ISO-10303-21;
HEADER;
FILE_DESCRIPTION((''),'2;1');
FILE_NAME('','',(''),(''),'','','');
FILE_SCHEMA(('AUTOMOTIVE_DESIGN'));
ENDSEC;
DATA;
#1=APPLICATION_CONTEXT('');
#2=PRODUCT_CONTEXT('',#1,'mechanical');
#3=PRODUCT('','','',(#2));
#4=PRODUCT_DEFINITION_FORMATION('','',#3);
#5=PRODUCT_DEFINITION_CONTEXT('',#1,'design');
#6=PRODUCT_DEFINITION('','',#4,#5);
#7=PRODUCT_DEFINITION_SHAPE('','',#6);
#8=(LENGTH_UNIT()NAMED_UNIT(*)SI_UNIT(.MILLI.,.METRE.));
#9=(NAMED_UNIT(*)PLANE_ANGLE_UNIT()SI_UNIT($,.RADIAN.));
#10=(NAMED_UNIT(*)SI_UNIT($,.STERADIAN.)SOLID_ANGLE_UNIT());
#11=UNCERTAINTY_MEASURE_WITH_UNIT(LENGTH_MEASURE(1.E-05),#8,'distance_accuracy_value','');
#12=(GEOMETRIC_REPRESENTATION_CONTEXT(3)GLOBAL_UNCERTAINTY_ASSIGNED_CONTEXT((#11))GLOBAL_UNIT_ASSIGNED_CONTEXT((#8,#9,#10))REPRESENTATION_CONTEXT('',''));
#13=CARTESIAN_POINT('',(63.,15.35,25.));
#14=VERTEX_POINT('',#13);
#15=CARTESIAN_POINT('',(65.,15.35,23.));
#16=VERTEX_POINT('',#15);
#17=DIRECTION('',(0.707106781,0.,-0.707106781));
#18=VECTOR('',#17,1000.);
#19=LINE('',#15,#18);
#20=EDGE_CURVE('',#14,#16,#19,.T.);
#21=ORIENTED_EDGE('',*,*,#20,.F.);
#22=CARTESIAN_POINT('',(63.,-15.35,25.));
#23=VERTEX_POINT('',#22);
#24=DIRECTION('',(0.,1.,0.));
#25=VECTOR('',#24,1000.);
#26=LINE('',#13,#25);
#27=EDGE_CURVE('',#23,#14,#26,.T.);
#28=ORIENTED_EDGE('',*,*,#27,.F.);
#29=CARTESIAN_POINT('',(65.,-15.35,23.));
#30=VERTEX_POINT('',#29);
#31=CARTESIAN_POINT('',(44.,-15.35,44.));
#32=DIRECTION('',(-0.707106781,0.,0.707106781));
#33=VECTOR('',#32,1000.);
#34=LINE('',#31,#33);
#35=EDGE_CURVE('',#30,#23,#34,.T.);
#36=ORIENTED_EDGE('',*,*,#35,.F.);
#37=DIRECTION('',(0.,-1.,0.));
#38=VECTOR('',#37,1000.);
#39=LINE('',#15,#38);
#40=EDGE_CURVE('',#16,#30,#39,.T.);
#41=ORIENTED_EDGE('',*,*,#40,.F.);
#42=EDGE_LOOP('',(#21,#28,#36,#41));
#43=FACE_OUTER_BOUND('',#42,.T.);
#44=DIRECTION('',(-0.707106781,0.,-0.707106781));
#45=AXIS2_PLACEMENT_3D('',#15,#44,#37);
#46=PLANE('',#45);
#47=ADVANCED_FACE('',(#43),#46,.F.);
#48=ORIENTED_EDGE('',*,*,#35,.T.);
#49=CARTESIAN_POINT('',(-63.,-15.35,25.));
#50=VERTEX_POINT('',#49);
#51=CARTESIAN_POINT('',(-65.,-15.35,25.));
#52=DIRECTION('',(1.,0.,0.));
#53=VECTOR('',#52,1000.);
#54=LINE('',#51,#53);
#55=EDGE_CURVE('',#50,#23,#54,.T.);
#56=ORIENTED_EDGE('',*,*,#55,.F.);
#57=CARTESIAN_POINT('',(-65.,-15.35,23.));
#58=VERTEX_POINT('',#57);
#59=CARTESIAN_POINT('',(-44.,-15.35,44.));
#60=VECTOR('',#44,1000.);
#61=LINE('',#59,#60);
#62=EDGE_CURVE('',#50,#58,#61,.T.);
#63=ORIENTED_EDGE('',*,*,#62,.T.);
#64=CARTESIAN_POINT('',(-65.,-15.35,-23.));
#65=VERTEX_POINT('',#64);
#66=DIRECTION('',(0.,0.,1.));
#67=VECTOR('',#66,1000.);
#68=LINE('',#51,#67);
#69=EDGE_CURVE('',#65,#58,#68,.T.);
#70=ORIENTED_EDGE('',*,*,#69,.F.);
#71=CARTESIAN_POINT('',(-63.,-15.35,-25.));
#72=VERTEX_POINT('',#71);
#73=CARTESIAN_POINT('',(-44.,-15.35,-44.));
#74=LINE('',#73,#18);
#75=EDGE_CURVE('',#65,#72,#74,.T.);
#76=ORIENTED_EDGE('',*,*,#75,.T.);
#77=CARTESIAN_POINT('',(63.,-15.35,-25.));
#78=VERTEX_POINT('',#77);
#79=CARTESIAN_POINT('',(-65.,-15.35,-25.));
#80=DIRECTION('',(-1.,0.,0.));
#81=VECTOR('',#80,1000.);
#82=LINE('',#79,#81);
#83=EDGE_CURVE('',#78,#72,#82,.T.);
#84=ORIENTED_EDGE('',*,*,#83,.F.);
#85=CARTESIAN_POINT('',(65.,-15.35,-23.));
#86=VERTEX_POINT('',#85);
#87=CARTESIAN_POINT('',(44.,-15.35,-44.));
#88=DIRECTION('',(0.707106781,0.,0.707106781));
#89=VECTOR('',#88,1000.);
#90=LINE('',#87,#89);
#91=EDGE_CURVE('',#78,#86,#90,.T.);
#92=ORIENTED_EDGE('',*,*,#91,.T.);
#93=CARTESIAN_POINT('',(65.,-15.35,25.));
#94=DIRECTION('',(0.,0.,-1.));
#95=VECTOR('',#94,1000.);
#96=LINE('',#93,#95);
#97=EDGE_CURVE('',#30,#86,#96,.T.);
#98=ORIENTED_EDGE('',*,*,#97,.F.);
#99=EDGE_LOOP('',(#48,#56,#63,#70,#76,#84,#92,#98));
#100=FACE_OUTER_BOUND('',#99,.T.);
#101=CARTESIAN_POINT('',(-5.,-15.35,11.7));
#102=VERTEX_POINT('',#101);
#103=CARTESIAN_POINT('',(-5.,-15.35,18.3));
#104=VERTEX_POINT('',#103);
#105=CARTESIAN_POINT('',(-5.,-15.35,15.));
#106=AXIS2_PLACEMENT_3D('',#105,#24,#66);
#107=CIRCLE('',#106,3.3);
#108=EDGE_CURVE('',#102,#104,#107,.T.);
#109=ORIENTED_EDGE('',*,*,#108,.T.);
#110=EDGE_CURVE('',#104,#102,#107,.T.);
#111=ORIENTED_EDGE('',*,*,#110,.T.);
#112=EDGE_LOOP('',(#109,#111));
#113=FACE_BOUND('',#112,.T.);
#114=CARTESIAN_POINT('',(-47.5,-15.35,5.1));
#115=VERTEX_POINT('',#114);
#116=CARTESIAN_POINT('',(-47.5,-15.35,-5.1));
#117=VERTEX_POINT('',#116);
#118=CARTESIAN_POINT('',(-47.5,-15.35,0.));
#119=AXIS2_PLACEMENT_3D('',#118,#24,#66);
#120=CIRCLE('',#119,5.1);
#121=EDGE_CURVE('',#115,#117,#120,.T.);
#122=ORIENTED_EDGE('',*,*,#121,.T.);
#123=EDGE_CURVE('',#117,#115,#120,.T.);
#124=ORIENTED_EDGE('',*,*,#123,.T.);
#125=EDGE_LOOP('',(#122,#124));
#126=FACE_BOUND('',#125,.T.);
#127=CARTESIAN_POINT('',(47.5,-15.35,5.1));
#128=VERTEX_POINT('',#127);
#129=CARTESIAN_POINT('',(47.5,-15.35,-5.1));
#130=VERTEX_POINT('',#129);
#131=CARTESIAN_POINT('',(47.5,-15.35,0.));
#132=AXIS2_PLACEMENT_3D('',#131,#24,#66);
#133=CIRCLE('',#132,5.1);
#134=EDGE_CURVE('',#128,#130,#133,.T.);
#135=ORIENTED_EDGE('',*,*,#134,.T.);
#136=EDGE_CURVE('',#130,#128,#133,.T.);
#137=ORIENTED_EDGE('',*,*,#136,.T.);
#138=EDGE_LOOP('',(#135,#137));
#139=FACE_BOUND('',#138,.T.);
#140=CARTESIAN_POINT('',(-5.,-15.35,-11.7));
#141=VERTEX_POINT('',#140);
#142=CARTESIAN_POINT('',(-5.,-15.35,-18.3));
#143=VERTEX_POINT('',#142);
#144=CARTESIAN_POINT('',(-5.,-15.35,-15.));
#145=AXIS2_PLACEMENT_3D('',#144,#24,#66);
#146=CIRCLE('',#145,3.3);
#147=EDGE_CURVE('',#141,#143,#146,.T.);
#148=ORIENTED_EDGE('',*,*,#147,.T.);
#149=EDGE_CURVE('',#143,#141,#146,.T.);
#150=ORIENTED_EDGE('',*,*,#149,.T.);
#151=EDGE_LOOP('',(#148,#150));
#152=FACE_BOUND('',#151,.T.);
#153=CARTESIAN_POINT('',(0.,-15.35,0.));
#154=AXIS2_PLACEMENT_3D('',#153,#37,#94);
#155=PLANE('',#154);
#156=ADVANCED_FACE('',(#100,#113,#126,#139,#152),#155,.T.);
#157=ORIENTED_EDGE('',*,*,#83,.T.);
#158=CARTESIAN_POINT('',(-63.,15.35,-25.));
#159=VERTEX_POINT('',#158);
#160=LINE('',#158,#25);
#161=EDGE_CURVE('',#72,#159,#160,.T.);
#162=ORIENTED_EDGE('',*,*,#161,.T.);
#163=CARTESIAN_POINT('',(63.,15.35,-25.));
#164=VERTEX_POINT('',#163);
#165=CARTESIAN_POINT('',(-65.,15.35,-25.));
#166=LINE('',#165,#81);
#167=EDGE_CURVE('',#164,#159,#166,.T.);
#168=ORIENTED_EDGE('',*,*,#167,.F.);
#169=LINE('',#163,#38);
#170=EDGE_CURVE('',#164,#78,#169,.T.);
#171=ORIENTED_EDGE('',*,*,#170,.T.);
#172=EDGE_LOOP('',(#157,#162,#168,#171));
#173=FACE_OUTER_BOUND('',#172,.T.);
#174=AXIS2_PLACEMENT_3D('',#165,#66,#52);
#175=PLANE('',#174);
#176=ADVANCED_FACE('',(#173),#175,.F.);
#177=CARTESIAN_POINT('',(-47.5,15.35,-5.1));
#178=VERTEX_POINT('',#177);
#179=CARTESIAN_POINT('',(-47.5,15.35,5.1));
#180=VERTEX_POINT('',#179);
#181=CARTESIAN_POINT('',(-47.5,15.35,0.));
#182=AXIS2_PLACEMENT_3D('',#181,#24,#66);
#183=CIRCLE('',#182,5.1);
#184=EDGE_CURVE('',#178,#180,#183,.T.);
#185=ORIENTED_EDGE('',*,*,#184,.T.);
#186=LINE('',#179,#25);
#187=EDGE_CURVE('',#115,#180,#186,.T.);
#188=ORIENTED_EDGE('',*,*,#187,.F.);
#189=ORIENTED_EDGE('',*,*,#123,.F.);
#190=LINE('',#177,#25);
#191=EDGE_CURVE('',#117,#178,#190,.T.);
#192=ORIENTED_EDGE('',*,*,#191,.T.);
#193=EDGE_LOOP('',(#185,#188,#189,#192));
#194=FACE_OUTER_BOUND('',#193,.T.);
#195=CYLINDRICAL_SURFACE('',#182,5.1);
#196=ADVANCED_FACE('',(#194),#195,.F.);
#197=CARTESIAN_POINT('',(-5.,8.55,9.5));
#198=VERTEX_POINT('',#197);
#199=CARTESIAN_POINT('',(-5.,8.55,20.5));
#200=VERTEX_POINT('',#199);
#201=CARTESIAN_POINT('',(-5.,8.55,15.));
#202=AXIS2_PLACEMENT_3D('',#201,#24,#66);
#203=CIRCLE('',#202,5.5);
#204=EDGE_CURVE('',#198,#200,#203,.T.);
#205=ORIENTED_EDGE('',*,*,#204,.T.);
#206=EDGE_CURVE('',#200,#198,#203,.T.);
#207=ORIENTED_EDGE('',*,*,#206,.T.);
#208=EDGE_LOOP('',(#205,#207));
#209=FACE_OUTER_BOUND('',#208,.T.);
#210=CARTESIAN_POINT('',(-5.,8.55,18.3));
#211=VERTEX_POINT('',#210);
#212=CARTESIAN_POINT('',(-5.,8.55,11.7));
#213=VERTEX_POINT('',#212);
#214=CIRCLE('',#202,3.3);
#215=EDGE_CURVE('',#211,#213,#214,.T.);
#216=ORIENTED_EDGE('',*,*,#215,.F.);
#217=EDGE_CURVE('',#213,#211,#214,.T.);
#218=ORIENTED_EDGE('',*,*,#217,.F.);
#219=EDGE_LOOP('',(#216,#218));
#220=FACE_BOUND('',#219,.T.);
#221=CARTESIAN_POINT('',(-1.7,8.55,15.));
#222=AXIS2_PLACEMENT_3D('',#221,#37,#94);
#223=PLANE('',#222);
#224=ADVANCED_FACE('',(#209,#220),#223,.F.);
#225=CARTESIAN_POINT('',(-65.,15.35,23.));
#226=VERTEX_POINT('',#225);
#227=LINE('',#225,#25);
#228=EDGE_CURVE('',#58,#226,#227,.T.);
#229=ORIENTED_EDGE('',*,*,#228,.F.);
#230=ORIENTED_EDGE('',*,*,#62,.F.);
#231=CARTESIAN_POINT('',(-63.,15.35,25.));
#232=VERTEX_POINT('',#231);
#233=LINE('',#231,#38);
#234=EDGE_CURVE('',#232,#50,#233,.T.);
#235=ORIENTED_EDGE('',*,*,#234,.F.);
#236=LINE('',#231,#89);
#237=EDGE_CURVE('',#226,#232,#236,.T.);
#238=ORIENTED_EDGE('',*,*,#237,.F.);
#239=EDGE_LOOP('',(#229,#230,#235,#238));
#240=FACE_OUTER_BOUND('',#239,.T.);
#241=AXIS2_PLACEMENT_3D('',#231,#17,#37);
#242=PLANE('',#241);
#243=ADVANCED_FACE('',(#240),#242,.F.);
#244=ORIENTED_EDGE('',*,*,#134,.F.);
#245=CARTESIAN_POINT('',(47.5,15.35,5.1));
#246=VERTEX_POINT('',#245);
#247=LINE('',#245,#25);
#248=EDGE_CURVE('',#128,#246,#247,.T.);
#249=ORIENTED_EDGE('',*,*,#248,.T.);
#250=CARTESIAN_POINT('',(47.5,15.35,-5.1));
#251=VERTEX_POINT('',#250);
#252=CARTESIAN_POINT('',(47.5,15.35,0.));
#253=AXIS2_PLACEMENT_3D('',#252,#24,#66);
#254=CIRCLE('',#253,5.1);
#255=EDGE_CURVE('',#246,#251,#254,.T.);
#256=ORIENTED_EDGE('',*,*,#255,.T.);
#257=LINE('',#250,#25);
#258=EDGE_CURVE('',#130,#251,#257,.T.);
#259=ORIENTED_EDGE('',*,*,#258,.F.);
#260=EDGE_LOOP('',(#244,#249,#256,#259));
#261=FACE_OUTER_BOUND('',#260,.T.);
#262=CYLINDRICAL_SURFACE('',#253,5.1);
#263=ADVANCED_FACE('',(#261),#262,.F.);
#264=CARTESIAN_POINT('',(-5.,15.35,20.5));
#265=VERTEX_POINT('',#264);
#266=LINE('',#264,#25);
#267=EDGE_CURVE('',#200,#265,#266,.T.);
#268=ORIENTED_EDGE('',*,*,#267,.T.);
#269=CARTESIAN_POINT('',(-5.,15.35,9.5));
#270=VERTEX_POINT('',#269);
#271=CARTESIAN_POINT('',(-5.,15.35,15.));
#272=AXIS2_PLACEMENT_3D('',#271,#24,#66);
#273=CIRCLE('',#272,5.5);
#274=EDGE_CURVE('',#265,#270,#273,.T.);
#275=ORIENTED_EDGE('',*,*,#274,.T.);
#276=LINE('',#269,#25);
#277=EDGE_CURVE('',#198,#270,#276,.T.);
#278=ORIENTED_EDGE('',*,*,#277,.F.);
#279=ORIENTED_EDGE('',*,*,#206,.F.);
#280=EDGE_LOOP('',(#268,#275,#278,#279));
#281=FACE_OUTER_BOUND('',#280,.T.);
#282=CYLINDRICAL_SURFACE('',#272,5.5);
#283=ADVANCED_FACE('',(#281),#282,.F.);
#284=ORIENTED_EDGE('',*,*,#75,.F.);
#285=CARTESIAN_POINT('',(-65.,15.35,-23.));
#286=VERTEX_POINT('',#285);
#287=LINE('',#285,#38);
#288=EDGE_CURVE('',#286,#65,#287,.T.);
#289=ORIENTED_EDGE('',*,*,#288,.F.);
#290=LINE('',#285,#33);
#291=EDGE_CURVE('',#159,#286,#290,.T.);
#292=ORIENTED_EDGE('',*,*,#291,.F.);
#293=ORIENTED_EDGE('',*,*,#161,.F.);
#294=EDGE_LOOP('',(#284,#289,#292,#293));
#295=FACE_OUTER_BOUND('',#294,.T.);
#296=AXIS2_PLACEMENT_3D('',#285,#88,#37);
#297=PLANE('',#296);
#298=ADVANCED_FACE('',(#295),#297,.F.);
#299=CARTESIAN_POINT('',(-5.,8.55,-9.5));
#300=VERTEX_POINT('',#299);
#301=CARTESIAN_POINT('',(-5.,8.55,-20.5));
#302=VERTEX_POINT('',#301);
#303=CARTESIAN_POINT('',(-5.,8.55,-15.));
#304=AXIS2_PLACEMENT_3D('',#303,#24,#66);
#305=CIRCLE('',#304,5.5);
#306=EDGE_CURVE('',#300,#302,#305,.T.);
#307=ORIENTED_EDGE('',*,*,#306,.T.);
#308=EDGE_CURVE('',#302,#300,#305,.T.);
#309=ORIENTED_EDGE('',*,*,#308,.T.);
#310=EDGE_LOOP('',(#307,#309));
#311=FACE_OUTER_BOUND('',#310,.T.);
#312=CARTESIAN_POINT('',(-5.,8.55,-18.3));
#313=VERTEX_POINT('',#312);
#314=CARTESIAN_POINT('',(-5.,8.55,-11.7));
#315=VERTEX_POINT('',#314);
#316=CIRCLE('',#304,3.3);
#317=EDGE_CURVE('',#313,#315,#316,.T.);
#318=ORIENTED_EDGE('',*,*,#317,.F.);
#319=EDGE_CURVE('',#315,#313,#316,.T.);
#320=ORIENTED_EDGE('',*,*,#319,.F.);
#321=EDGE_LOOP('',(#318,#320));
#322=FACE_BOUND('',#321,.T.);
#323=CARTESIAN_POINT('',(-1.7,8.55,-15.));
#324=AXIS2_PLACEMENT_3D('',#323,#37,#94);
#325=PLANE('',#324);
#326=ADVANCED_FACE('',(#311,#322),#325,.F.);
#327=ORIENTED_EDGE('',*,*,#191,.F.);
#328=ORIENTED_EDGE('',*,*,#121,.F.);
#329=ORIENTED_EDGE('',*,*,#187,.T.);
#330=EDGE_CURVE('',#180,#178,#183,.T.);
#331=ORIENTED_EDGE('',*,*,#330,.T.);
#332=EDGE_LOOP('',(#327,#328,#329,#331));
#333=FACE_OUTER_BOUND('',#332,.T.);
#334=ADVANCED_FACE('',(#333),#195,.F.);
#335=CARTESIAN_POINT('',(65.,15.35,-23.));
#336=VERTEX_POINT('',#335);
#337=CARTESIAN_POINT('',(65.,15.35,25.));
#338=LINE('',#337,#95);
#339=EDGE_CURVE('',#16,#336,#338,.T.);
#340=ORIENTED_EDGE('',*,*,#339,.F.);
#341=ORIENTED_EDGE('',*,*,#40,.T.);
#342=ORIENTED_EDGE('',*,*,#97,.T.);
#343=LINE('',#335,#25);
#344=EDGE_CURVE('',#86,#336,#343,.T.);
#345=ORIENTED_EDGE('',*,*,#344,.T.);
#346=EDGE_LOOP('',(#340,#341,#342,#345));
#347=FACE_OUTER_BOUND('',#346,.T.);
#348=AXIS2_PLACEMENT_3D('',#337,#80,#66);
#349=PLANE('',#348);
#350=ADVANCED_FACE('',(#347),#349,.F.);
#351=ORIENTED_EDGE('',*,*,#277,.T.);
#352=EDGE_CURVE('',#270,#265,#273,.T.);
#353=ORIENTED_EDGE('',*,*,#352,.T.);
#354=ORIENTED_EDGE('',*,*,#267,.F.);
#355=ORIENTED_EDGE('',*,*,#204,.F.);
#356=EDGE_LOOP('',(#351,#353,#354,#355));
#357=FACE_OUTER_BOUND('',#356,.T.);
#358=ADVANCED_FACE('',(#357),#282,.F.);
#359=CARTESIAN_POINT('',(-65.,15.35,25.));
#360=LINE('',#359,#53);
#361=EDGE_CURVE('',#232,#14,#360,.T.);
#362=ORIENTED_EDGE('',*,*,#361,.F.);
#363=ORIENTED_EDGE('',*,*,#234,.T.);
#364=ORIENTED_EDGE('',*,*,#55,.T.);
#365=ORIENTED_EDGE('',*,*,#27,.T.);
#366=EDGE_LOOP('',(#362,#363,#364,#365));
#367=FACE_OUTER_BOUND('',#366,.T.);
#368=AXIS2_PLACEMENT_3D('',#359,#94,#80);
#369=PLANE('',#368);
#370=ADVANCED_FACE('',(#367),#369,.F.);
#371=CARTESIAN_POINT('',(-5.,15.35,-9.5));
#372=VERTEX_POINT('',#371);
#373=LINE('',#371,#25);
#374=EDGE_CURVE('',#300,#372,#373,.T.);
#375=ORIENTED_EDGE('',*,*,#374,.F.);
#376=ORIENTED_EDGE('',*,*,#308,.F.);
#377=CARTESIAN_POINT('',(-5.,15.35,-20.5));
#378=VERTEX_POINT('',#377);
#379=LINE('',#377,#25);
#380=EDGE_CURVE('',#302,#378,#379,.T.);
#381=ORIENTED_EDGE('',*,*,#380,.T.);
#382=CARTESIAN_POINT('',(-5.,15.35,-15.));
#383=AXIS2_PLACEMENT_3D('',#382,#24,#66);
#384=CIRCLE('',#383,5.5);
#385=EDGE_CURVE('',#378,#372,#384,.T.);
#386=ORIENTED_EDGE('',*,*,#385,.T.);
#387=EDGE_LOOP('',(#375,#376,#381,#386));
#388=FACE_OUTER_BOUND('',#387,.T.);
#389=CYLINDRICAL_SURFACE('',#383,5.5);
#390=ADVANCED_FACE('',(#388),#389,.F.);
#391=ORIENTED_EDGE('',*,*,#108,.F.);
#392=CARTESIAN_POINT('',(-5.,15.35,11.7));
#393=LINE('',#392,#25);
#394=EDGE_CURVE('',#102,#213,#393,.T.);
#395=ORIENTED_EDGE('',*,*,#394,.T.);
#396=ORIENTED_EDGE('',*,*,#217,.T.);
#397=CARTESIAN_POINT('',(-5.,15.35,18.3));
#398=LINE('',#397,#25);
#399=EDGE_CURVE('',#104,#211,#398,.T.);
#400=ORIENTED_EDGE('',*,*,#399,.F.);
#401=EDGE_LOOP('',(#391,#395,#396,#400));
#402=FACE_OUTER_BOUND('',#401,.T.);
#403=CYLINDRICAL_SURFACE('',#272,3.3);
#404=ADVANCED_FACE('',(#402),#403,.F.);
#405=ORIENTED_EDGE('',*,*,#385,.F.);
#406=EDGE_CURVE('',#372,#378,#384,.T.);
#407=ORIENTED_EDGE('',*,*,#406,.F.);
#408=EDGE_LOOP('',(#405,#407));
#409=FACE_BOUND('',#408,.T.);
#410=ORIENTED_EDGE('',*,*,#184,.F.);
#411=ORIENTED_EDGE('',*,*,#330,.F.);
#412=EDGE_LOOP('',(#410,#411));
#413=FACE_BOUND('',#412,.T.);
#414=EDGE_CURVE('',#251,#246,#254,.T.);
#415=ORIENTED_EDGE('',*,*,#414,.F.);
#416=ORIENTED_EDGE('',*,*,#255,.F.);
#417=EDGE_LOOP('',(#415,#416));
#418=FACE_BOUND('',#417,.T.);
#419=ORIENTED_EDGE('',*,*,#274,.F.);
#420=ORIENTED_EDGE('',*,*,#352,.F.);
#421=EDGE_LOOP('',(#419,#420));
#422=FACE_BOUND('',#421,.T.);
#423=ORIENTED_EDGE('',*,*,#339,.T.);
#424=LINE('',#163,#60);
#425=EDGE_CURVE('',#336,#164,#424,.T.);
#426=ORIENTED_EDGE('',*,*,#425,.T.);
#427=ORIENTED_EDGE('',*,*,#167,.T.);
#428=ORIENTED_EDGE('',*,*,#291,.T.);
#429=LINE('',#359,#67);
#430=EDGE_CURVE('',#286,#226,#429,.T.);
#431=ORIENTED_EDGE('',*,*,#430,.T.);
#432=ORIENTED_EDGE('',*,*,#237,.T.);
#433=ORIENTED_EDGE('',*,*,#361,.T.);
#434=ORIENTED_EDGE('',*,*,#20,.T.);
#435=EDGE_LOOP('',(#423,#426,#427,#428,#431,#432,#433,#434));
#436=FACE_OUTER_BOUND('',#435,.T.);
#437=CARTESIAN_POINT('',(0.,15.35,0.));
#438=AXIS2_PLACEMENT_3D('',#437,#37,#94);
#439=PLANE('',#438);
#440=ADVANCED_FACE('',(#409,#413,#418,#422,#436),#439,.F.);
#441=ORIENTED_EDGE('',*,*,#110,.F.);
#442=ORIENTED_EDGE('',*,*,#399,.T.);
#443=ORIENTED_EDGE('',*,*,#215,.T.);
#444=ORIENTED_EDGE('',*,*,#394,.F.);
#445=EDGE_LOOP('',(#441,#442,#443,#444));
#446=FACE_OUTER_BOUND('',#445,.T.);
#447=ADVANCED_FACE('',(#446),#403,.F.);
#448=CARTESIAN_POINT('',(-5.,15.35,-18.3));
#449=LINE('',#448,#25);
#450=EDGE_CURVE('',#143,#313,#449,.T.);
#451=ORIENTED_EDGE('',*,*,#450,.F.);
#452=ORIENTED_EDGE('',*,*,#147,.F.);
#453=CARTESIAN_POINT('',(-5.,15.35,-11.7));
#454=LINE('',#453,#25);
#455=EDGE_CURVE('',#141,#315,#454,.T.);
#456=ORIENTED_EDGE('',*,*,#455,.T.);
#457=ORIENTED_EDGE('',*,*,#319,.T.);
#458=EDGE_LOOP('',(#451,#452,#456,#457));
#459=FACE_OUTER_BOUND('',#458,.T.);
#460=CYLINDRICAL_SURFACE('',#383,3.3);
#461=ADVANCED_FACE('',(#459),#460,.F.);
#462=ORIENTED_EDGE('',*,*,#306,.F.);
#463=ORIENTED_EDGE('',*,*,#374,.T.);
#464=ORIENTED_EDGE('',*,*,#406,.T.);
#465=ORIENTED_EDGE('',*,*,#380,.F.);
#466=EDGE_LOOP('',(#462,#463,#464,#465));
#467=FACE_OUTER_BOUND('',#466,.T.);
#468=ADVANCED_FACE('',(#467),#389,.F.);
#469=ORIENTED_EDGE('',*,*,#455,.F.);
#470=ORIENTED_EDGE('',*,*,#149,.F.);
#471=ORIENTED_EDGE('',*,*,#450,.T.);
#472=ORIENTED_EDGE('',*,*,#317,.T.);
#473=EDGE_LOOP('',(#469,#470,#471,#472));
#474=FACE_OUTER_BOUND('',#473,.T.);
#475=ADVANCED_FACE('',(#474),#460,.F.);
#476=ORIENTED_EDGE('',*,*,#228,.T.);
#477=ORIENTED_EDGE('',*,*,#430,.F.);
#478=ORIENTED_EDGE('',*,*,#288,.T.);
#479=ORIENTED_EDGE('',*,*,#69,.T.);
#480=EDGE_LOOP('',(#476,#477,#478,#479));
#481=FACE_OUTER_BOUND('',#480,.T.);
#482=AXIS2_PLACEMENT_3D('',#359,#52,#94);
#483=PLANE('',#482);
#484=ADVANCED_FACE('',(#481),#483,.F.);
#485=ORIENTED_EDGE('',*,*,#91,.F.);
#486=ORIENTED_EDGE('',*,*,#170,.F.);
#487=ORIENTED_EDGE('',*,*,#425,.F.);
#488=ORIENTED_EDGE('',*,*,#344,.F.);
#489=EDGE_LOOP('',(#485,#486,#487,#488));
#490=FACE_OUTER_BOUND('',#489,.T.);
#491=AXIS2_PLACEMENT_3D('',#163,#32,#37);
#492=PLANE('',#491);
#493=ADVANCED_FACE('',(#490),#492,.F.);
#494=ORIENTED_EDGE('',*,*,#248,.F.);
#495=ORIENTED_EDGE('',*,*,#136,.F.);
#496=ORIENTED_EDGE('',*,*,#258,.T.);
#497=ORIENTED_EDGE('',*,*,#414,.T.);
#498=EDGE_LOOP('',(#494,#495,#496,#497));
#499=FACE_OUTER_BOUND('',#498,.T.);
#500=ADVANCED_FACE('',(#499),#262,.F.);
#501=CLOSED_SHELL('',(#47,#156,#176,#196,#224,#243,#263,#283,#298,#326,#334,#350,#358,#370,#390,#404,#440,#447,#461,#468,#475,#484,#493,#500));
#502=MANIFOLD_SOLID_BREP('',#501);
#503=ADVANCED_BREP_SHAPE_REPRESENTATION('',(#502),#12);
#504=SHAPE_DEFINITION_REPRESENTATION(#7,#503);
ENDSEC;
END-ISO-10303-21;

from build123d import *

# Parameters (mm, degrees)
SKETCH_1_W                = 130
SKETCH_1_H                = 50
EXTRUDE_1_DEPTH           = 15.35
CHAMFER_1_SIZE            = 2
HOLE_WIZARD_M12_1_D       = 10.2
HOLE_WIZARD_1_D           = 6.6
HOLE_WIZARD_1_CBORE_D     = 11
HOLE_WIZARD_1_CBORE_DEPTH = 6.8


with BuildPart() as part:
    # 草图1 → 凸台-拉伸1 (new, symmetric)
    with BuildSketch(Plane(origin=(0, 0, 0), x_dir=(1, 0, 0), z_dir=(0, 1, 0))):
        Rectangle(SKETCH_1_W, SKETCH_1_H)
    extrude(amount=EXTRUDE_1_DEPTH, both=True)

    # 倒角1
    chamfer_1_edges = [part.edges().sort_by_distance(p)[0] for p in [
        (65, 0, 25),
        (-65, 0, 25),
        (-65, 0, -25),
        (65, 0, -25),
    ]]
    chamfer(chamfer_1_edges, length=CHAMFER_1_SIZE)

    # M12 螺纹孔1 (through all)
    with Locations(Plane(origin=(0, 15.35, 0), x_dir=(1, 0, 0), z_dir=(0, 1, 0))):
        with Locations((-47.5, 0), (47.5, 0)):
            Hole(HOLE_WIZARD_M12_1_D / 2)

    # 打孔尺寸(%根据)内六角圆柱头螺钉的类型1 (through all)
    with Locations(Plane(origin=(0, 15.35, 0), x_dir=(1, 0, 0), z_dir=(0, 1, 0))):
        with Locations((-5, -15), (-5, 15)):
            CounterBoreHole(HOLE_WIZARD_1_D / 2, HOLE_WIZARD_1_CBORE_D / 2, HOLE_WIZARD_1_CBORE_DEPTH)


solid = part.part
